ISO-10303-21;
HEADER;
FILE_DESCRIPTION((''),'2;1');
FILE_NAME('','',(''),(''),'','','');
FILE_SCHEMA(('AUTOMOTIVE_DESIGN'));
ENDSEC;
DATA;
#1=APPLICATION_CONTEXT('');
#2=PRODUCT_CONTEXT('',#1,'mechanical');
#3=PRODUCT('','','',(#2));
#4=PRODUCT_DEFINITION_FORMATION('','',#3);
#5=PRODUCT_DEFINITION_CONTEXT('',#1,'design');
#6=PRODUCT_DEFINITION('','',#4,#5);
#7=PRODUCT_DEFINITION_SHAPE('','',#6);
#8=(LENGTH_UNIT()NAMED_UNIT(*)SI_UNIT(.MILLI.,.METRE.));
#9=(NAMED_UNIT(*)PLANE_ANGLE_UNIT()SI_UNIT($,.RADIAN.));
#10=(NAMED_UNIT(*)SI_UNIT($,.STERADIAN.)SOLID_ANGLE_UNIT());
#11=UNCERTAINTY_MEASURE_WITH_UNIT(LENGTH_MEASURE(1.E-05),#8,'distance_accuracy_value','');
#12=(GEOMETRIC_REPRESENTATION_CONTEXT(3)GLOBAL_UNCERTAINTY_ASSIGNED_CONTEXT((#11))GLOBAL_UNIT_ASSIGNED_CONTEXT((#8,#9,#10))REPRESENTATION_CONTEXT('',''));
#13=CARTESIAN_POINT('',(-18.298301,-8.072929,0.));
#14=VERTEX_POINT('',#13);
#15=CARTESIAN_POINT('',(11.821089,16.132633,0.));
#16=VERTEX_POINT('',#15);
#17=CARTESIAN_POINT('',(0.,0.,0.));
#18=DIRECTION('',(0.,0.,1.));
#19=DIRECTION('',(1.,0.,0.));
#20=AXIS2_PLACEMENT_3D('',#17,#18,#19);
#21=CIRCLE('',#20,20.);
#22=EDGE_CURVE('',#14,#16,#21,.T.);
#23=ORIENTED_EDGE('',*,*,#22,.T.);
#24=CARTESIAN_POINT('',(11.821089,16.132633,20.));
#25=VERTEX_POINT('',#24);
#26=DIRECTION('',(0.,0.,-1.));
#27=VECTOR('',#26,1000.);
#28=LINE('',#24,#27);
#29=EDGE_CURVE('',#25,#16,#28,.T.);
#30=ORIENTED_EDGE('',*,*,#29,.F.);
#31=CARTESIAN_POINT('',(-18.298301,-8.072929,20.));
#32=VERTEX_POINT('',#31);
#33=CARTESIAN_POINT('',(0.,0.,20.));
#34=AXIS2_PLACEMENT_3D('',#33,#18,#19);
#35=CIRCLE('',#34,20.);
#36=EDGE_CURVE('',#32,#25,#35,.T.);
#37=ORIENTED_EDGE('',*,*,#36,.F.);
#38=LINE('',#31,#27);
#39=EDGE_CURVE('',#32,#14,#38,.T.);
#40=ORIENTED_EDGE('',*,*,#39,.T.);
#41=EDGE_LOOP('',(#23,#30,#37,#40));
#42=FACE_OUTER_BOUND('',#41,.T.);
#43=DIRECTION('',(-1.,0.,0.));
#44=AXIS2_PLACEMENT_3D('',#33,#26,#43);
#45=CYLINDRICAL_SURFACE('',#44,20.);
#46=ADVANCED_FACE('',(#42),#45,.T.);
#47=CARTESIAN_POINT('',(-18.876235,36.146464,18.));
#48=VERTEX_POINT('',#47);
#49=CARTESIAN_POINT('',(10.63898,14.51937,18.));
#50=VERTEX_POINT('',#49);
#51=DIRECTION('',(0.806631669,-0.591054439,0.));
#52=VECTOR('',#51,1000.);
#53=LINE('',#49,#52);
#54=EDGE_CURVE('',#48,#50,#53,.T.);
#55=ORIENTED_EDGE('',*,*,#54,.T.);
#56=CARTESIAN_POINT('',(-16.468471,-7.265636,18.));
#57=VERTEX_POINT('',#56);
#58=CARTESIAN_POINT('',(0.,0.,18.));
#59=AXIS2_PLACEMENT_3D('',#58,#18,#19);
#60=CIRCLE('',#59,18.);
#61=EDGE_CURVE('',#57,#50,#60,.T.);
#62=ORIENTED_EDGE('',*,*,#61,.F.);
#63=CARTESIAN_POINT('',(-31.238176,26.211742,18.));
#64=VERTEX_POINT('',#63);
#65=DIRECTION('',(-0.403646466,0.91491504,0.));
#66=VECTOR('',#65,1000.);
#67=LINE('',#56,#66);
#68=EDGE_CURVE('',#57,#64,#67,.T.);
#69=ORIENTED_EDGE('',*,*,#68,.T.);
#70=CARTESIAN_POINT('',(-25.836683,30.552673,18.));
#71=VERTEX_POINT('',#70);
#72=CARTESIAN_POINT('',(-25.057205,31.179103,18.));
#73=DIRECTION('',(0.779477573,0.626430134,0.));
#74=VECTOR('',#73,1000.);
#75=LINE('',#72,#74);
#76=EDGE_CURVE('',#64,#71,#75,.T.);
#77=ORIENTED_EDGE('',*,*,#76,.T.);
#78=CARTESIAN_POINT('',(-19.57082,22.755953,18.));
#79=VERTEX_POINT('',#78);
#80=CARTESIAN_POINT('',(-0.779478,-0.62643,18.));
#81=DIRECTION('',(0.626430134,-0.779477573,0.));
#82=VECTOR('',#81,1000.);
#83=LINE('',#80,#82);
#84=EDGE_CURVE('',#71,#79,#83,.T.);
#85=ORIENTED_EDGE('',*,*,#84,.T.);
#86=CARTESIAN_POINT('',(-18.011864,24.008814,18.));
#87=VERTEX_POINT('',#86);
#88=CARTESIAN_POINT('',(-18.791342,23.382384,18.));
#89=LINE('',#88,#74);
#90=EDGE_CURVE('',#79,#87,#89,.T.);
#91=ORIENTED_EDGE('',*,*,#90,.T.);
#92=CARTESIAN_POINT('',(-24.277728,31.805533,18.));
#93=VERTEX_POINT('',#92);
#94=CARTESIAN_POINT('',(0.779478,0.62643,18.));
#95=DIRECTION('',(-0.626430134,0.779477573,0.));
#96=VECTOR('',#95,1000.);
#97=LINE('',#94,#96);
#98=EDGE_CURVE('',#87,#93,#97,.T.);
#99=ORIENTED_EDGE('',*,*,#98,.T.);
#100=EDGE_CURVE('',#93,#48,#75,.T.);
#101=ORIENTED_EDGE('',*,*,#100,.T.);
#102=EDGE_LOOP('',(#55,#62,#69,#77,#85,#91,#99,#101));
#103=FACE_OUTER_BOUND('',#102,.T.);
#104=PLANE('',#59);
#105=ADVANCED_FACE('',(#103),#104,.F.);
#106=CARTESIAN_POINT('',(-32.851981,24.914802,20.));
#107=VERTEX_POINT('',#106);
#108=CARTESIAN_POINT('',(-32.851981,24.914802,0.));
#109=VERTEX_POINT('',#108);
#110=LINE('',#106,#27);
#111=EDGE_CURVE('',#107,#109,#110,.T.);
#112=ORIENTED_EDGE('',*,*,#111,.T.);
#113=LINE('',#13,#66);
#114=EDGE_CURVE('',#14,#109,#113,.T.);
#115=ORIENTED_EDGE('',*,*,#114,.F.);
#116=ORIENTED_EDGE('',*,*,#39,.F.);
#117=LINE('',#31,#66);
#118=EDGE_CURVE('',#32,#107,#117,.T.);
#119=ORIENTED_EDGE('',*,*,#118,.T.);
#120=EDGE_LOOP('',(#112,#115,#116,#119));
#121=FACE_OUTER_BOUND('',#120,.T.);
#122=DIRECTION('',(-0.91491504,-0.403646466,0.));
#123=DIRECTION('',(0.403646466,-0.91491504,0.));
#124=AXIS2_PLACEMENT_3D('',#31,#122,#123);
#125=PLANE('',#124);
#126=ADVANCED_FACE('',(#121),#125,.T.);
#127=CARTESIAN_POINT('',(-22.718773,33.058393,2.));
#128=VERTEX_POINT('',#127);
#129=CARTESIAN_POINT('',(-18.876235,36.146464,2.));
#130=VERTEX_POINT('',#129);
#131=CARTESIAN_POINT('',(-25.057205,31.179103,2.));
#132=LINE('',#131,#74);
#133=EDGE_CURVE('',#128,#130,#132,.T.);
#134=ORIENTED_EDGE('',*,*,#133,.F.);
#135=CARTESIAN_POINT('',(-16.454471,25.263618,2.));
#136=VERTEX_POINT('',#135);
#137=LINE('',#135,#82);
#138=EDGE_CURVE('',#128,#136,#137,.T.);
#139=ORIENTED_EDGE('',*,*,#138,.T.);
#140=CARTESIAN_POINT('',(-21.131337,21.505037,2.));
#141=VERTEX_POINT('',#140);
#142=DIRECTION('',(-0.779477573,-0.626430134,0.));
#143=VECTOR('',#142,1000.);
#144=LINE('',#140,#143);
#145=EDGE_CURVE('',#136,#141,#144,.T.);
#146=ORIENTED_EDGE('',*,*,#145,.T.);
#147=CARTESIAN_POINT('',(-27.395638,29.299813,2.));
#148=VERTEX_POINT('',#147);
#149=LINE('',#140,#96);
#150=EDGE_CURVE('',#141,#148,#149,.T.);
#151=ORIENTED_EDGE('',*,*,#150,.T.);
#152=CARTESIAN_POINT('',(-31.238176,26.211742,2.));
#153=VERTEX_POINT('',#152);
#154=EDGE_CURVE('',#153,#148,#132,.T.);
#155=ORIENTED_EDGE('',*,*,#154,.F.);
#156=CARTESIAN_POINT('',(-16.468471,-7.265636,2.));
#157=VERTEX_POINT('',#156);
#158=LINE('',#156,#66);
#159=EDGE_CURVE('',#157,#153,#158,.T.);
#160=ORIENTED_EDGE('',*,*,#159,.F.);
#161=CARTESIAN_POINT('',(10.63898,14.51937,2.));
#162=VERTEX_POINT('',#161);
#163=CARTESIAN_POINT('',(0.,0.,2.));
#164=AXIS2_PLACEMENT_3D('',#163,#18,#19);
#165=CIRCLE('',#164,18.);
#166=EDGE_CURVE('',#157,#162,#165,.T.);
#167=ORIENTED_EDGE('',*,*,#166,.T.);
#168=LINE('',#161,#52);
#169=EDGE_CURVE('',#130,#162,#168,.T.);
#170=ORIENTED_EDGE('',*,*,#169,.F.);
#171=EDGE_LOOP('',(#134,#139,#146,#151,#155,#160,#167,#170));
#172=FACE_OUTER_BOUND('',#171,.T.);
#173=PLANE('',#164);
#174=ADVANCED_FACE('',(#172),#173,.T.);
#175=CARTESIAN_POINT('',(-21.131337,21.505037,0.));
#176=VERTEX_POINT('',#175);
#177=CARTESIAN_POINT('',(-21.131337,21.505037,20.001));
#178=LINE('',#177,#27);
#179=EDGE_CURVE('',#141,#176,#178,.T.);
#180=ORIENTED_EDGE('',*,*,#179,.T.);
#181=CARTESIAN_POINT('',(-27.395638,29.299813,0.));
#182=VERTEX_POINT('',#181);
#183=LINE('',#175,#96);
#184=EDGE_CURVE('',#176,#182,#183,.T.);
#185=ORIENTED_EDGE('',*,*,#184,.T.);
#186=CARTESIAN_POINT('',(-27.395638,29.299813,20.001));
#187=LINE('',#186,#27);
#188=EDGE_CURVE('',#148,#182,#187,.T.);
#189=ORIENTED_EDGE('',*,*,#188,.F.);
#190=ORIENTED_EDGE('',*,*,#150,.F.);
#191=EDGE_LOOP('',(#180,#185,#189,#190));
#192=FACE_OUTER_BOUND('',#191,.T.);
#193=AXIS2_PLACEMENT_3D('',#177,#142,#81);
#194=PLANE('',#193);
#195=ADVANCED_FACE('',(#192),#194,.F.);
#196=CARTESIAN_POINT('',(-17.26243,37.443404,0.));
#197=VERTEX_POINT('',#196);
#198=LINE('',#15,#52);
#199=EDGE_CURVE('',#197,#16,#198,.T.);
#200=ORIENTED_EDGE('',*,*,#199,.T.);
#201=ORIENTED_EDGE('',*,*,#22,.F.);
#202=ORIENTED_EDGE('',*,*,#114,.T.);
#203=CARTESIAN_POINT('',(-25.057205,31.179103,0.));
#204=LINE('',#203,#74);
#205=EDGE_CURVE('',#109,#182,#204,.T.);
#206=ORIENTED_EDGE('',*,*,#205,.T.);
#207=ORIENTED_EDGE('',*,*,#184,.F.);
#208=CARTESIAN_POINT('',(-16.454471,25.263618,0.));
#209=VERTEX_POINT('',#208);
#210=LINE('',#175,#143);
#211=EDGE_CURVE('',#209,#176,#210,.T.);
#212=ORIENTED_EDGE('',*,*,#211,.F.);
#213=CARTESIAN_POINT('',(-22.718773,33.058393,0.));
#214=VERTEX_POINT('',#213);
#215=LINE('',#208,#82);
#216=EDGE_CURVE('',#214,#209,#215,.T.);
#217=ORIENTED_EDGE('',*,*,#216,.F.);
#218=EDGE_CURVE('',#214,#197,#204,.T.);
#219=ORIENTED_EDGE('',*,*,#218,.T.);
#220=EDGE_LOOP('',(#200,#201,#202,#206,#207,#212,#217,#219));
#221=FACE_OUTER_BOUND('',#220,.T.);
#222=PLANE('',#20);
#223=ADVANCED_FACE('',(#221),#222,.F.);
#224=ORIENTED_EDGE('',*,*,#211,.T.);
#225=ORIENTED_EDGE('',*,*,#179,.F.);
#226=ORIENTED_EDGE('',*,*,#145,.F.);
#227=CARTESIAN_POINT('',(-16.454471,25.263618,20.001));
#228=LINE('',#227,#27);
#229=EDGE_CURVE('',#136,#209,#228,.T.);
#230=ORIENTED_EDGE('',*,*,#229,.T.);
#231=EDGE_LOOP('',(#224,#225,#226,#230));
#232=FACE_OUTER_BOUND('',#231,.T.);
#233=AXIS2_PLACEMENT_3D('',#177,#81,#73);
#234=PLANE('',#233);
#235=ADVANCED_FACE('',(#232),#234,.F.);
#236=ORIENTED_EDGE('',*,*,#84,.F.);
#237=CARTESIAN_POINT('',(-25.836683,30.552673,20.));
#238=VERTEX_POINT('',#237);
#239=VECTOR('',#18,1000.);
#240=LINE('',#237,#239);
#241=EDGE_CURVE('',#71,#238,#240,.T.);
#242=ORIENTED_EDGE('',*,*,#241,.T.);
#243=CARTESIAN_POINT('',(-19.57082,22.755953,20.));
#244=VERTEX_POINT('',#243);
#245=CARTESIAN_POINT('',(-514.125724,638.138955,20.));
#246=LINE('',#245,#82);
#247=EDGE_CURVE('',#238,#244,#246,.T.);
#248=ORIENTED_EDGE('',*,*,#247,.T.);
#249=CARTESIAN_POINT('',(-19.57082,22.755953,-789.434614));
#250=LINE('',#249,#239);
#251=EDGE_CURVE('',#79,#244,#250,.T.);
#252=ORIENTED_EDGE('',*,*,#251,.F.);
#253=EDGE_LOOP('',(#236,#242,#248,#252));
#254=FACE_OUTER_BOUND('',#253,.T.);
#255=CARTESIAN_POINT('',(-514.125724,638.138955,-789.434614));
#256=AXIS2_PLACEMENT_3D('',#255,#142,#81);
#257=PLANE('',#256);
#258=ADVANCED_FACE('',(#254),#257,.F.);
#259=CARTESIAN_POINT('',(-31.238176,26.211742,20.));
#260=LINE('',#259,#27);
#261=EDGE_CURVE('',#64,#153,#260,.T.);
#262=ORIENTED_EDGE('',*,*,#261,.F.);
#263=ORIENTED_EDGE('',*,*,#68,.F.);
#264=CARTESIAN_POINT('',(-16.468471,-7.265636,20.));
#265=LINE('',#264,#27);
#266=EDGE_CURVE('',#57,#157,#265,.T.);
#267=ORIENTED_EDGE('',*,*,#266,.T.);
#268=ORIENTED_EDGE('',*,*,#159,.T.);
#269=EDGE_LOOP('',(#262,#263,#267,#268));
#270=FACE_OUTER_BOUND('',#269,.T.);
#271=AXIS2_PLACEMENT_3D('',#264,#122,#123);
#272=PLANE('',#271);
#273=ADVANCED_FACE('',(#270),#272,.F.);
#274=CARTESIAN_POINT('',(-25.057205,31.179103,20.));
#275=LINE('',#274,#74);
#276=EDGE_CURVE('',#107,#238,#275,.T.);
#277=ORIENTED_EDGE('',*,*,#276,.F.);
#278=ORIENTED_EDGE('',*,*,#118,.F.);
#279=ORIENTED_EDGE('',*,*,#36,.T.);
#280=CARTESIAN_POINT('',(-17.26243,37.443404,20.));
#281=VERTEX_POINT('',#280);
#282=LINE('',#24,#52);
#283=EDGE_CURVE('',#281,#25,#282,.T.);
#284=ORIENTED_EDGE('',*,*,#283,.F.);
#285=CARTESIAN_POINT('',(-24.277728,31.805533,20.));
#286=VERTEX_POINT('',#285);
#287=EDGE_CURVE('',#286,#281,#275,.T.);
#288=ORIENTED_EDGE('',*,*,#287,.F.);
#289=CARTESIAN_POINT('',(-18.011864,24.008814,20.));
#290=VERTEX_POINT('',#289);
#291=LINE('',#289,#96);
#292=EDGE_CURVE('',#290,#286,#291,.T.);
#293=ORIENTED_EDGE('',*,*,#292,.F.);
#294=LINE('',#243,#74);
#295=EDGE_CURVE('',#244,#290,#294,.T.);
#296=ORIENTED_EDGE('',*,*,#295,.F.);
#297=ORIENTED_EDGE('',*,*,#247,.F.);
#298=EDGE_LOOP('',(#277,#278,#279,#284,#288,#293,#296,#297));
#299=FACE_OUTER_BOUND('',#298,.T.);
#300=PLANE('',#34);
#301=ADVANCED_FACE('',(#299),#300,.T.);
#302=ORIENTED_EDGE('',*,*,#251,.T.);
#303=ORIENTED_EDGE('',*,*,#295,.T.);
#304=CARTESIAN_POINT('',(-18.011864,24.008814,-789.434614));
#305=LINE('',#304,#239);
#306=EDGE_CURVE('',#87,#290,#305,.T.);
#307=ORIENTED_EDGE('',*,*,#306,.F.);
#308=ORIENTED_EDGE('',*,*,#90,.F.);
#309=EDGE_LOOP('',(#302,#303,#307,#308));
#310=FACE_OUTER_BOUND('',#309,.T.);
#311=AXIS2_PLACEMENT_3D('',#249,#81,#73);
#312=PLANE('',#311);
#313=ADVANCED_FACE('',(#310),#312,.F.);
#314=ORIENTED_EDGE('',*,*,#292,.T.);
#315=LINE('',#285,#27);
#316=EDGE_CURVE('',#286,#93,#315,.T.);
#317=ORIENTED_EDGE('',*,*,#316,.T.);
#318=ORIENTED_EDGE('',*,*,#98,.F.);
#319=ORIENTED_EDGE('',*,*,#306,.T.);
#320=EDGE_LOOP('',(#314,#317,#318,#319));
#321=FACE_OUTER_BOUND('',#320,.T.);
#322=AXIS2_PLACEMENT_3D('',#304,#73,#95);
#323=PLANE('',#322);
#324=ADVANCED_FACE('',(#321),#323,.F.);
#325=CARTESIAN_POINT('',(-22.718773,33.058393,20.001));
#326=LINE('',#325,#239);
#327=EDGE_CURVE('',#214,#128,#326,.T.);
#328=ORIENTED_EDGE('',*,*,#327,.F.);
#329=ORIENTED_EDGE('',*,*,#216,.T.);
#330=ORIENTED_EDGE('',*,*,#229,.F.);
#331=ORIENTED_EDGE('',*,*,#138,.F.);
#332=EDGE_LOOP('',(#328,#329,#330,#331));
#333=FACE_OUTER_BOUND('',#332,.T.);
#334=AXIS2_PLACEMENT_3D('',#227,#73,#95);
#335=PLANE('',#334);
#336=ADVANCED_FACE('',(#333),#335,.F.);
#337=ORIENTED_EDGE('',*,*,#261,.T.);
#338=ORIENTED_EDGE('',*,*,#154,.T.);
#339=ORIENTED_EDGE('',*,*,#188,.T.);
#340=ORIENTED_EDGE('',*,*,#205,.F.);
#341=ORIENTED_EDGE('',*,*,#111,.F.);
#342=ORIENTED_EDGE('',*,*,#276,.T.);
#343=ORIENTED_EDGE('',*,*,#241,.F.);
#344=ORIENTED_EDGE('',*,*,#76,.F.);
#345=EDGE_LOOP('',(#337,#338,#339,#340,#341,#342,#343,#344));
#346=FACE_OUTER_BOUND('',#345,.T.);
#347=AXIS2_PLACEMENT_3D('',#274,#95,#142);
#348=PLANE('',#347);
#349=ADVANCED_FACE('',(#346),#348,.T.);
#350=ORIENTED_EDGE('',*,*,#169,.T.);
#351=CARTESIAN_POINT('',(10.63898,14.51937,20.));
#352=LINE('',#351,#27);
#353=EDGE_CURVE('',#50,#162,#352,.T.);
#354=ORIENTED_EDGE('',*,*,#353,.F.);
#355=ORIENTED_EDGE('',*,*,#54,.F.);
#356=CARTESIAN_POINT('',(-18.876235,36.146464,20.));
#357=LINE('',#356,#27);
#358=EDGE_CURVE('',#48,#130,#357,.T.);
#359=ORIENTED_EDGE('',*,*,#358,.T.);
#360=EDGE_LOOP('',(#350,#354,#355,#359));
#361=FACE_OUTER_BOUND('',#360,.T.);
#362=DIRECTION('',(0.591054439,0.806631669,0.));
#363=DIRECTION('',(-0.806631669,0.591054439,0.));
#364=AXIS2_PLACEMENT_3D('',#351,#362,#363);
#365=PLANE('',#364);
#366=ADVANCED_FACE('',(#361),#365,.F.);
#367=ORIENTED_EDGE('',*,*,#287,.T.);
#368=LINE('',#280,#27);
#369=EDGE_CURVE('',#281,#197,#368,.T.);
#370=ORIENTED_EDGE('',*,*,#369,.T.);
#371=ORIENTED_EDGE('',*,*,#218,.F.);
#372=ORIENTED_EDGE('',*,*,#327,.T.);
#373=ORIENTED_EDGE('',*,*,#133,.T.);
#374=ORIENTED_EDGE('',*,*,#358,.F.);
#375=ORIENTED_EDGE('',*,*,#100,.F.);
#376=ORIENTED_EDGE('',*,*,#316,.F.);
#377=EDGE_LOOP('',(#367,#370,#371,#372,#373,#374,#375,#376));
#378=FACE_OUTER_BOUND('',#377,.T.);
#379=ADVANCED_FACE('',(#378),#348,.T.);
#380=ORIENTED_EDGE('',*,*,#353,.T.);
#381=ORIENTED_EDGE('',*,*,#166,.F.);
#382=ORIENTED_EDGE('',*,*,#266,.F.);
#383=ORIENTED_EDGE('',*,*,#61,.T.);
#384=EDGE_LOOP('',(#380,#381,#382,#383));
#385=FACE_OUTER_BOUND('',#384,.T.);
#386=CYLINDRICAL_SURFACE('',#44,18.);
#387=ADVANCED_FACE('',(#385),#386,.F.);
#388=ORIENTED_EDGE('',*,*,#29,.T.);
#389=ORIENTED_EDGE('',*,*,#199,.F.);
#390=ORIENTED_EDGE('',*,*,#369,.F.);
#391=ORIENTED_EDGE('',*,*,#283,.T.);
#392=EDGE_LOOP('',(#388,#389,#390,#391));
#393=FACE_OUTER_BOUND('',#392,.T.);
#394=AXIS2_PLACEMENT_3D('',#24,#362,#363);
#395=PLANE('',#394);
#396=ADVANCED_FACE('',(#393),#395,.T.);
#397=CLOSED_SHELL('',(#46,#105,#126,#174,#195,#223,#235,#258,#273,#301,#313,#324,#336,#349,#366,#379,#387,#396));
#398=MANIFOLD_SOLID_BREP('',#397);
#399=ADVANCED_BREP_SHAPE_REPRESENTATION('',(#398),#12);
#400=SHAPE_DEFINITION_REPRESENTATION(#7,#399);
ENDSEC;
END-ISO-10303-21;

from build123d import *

# Parameters (mm, degrees)
BOSS_EXTRUDE1_DEPTH = 20
SHELL1_T            = -2
CUT_EXTRUDE1_REACH  = 55.677
CUT_EXTRUDE2_REACH  = 55.677


with BuildPart() as part:
    # Sketch1 → Boss-Extrude1 (new body)
    with BuildSketch(Plane.XY):
        with BuildLine():
            Line((-32.851981106, 24.914801572), (-18.2983008, -8.072929322))
            ThreePointArc((-18.2983008, -8.072929322), (12.528602689, -15.589551458), (11.821088788, 16.132633383))
            Line((11.821088788, 16.132633383), (-17.262429648, 37.443404261))
            Line((-17.262429648, 37.443404261), (-32.851981106, 24.914801572))
        make_face()
    extrude(amount=BOSS_EXTRUDE1_DEPTH)

    # Shell1
    shell1_openings = [part.faces().sort_by_distance(p)[0] for p in [
        (-25.057205377, 31.179102917, 10),
    ]]
    offset(amount=SHELL1_T, openings=shell1_openings, kind=Kind.INTERSECTION)

    # Sketch2 → Cut-Extrude1 (cut, up to next)
    with BuildSketch(Plane(origin=(0, 0, 0), x_dir=(-1, 0, 0), z_dir=(0, 0, -1)), mode=Mode.PRIVATE) as cut_extrude1_sk1:
        Polygon((21.131336752, 21.505036784), (16.454471314, 25.263617591), (28.983074003, 40.853169049), (33.65993944, 37.094588242), align=None)
    cut_extrude1_tool1 = extrude(cut_extrude1_sk1.sketch, amount=-CUT_EXTRUDE1_REACH, mode=Mode.PRIVATE) & part.part
    add(cut_extrude1_tool1.solids().sort_by_distance((-25.057205, 31.179103, 0))[0], mode=Mode.SUBTRACT)

    # Sketch3 → Cut-Extrude2 (cut, up to next)
    with BuildSketch(Plane.XY.offset(20), mode=Mode.PRIVATE) as cut_extrude2_sk1:
        Polygon((-18.011864488, 24.008813734), (-512.566768876, 639.391815534), (-514.125724022, 638.138955265), (-19.570819634, 22.755953465), align=None)
    cut_extrude2_tool1 = extrude(cut_extrude2_sk1.sketch, amount=-CUT_EXTRUDE2_REACH, mode=Mode.PRIVATE) & part.part
    add(cut_extrude2_tool1.solids().sort_by_distance((-266.068794, 331.073884, 20))[0], mode=Mode.SUBTRACT)


solid = part.part
